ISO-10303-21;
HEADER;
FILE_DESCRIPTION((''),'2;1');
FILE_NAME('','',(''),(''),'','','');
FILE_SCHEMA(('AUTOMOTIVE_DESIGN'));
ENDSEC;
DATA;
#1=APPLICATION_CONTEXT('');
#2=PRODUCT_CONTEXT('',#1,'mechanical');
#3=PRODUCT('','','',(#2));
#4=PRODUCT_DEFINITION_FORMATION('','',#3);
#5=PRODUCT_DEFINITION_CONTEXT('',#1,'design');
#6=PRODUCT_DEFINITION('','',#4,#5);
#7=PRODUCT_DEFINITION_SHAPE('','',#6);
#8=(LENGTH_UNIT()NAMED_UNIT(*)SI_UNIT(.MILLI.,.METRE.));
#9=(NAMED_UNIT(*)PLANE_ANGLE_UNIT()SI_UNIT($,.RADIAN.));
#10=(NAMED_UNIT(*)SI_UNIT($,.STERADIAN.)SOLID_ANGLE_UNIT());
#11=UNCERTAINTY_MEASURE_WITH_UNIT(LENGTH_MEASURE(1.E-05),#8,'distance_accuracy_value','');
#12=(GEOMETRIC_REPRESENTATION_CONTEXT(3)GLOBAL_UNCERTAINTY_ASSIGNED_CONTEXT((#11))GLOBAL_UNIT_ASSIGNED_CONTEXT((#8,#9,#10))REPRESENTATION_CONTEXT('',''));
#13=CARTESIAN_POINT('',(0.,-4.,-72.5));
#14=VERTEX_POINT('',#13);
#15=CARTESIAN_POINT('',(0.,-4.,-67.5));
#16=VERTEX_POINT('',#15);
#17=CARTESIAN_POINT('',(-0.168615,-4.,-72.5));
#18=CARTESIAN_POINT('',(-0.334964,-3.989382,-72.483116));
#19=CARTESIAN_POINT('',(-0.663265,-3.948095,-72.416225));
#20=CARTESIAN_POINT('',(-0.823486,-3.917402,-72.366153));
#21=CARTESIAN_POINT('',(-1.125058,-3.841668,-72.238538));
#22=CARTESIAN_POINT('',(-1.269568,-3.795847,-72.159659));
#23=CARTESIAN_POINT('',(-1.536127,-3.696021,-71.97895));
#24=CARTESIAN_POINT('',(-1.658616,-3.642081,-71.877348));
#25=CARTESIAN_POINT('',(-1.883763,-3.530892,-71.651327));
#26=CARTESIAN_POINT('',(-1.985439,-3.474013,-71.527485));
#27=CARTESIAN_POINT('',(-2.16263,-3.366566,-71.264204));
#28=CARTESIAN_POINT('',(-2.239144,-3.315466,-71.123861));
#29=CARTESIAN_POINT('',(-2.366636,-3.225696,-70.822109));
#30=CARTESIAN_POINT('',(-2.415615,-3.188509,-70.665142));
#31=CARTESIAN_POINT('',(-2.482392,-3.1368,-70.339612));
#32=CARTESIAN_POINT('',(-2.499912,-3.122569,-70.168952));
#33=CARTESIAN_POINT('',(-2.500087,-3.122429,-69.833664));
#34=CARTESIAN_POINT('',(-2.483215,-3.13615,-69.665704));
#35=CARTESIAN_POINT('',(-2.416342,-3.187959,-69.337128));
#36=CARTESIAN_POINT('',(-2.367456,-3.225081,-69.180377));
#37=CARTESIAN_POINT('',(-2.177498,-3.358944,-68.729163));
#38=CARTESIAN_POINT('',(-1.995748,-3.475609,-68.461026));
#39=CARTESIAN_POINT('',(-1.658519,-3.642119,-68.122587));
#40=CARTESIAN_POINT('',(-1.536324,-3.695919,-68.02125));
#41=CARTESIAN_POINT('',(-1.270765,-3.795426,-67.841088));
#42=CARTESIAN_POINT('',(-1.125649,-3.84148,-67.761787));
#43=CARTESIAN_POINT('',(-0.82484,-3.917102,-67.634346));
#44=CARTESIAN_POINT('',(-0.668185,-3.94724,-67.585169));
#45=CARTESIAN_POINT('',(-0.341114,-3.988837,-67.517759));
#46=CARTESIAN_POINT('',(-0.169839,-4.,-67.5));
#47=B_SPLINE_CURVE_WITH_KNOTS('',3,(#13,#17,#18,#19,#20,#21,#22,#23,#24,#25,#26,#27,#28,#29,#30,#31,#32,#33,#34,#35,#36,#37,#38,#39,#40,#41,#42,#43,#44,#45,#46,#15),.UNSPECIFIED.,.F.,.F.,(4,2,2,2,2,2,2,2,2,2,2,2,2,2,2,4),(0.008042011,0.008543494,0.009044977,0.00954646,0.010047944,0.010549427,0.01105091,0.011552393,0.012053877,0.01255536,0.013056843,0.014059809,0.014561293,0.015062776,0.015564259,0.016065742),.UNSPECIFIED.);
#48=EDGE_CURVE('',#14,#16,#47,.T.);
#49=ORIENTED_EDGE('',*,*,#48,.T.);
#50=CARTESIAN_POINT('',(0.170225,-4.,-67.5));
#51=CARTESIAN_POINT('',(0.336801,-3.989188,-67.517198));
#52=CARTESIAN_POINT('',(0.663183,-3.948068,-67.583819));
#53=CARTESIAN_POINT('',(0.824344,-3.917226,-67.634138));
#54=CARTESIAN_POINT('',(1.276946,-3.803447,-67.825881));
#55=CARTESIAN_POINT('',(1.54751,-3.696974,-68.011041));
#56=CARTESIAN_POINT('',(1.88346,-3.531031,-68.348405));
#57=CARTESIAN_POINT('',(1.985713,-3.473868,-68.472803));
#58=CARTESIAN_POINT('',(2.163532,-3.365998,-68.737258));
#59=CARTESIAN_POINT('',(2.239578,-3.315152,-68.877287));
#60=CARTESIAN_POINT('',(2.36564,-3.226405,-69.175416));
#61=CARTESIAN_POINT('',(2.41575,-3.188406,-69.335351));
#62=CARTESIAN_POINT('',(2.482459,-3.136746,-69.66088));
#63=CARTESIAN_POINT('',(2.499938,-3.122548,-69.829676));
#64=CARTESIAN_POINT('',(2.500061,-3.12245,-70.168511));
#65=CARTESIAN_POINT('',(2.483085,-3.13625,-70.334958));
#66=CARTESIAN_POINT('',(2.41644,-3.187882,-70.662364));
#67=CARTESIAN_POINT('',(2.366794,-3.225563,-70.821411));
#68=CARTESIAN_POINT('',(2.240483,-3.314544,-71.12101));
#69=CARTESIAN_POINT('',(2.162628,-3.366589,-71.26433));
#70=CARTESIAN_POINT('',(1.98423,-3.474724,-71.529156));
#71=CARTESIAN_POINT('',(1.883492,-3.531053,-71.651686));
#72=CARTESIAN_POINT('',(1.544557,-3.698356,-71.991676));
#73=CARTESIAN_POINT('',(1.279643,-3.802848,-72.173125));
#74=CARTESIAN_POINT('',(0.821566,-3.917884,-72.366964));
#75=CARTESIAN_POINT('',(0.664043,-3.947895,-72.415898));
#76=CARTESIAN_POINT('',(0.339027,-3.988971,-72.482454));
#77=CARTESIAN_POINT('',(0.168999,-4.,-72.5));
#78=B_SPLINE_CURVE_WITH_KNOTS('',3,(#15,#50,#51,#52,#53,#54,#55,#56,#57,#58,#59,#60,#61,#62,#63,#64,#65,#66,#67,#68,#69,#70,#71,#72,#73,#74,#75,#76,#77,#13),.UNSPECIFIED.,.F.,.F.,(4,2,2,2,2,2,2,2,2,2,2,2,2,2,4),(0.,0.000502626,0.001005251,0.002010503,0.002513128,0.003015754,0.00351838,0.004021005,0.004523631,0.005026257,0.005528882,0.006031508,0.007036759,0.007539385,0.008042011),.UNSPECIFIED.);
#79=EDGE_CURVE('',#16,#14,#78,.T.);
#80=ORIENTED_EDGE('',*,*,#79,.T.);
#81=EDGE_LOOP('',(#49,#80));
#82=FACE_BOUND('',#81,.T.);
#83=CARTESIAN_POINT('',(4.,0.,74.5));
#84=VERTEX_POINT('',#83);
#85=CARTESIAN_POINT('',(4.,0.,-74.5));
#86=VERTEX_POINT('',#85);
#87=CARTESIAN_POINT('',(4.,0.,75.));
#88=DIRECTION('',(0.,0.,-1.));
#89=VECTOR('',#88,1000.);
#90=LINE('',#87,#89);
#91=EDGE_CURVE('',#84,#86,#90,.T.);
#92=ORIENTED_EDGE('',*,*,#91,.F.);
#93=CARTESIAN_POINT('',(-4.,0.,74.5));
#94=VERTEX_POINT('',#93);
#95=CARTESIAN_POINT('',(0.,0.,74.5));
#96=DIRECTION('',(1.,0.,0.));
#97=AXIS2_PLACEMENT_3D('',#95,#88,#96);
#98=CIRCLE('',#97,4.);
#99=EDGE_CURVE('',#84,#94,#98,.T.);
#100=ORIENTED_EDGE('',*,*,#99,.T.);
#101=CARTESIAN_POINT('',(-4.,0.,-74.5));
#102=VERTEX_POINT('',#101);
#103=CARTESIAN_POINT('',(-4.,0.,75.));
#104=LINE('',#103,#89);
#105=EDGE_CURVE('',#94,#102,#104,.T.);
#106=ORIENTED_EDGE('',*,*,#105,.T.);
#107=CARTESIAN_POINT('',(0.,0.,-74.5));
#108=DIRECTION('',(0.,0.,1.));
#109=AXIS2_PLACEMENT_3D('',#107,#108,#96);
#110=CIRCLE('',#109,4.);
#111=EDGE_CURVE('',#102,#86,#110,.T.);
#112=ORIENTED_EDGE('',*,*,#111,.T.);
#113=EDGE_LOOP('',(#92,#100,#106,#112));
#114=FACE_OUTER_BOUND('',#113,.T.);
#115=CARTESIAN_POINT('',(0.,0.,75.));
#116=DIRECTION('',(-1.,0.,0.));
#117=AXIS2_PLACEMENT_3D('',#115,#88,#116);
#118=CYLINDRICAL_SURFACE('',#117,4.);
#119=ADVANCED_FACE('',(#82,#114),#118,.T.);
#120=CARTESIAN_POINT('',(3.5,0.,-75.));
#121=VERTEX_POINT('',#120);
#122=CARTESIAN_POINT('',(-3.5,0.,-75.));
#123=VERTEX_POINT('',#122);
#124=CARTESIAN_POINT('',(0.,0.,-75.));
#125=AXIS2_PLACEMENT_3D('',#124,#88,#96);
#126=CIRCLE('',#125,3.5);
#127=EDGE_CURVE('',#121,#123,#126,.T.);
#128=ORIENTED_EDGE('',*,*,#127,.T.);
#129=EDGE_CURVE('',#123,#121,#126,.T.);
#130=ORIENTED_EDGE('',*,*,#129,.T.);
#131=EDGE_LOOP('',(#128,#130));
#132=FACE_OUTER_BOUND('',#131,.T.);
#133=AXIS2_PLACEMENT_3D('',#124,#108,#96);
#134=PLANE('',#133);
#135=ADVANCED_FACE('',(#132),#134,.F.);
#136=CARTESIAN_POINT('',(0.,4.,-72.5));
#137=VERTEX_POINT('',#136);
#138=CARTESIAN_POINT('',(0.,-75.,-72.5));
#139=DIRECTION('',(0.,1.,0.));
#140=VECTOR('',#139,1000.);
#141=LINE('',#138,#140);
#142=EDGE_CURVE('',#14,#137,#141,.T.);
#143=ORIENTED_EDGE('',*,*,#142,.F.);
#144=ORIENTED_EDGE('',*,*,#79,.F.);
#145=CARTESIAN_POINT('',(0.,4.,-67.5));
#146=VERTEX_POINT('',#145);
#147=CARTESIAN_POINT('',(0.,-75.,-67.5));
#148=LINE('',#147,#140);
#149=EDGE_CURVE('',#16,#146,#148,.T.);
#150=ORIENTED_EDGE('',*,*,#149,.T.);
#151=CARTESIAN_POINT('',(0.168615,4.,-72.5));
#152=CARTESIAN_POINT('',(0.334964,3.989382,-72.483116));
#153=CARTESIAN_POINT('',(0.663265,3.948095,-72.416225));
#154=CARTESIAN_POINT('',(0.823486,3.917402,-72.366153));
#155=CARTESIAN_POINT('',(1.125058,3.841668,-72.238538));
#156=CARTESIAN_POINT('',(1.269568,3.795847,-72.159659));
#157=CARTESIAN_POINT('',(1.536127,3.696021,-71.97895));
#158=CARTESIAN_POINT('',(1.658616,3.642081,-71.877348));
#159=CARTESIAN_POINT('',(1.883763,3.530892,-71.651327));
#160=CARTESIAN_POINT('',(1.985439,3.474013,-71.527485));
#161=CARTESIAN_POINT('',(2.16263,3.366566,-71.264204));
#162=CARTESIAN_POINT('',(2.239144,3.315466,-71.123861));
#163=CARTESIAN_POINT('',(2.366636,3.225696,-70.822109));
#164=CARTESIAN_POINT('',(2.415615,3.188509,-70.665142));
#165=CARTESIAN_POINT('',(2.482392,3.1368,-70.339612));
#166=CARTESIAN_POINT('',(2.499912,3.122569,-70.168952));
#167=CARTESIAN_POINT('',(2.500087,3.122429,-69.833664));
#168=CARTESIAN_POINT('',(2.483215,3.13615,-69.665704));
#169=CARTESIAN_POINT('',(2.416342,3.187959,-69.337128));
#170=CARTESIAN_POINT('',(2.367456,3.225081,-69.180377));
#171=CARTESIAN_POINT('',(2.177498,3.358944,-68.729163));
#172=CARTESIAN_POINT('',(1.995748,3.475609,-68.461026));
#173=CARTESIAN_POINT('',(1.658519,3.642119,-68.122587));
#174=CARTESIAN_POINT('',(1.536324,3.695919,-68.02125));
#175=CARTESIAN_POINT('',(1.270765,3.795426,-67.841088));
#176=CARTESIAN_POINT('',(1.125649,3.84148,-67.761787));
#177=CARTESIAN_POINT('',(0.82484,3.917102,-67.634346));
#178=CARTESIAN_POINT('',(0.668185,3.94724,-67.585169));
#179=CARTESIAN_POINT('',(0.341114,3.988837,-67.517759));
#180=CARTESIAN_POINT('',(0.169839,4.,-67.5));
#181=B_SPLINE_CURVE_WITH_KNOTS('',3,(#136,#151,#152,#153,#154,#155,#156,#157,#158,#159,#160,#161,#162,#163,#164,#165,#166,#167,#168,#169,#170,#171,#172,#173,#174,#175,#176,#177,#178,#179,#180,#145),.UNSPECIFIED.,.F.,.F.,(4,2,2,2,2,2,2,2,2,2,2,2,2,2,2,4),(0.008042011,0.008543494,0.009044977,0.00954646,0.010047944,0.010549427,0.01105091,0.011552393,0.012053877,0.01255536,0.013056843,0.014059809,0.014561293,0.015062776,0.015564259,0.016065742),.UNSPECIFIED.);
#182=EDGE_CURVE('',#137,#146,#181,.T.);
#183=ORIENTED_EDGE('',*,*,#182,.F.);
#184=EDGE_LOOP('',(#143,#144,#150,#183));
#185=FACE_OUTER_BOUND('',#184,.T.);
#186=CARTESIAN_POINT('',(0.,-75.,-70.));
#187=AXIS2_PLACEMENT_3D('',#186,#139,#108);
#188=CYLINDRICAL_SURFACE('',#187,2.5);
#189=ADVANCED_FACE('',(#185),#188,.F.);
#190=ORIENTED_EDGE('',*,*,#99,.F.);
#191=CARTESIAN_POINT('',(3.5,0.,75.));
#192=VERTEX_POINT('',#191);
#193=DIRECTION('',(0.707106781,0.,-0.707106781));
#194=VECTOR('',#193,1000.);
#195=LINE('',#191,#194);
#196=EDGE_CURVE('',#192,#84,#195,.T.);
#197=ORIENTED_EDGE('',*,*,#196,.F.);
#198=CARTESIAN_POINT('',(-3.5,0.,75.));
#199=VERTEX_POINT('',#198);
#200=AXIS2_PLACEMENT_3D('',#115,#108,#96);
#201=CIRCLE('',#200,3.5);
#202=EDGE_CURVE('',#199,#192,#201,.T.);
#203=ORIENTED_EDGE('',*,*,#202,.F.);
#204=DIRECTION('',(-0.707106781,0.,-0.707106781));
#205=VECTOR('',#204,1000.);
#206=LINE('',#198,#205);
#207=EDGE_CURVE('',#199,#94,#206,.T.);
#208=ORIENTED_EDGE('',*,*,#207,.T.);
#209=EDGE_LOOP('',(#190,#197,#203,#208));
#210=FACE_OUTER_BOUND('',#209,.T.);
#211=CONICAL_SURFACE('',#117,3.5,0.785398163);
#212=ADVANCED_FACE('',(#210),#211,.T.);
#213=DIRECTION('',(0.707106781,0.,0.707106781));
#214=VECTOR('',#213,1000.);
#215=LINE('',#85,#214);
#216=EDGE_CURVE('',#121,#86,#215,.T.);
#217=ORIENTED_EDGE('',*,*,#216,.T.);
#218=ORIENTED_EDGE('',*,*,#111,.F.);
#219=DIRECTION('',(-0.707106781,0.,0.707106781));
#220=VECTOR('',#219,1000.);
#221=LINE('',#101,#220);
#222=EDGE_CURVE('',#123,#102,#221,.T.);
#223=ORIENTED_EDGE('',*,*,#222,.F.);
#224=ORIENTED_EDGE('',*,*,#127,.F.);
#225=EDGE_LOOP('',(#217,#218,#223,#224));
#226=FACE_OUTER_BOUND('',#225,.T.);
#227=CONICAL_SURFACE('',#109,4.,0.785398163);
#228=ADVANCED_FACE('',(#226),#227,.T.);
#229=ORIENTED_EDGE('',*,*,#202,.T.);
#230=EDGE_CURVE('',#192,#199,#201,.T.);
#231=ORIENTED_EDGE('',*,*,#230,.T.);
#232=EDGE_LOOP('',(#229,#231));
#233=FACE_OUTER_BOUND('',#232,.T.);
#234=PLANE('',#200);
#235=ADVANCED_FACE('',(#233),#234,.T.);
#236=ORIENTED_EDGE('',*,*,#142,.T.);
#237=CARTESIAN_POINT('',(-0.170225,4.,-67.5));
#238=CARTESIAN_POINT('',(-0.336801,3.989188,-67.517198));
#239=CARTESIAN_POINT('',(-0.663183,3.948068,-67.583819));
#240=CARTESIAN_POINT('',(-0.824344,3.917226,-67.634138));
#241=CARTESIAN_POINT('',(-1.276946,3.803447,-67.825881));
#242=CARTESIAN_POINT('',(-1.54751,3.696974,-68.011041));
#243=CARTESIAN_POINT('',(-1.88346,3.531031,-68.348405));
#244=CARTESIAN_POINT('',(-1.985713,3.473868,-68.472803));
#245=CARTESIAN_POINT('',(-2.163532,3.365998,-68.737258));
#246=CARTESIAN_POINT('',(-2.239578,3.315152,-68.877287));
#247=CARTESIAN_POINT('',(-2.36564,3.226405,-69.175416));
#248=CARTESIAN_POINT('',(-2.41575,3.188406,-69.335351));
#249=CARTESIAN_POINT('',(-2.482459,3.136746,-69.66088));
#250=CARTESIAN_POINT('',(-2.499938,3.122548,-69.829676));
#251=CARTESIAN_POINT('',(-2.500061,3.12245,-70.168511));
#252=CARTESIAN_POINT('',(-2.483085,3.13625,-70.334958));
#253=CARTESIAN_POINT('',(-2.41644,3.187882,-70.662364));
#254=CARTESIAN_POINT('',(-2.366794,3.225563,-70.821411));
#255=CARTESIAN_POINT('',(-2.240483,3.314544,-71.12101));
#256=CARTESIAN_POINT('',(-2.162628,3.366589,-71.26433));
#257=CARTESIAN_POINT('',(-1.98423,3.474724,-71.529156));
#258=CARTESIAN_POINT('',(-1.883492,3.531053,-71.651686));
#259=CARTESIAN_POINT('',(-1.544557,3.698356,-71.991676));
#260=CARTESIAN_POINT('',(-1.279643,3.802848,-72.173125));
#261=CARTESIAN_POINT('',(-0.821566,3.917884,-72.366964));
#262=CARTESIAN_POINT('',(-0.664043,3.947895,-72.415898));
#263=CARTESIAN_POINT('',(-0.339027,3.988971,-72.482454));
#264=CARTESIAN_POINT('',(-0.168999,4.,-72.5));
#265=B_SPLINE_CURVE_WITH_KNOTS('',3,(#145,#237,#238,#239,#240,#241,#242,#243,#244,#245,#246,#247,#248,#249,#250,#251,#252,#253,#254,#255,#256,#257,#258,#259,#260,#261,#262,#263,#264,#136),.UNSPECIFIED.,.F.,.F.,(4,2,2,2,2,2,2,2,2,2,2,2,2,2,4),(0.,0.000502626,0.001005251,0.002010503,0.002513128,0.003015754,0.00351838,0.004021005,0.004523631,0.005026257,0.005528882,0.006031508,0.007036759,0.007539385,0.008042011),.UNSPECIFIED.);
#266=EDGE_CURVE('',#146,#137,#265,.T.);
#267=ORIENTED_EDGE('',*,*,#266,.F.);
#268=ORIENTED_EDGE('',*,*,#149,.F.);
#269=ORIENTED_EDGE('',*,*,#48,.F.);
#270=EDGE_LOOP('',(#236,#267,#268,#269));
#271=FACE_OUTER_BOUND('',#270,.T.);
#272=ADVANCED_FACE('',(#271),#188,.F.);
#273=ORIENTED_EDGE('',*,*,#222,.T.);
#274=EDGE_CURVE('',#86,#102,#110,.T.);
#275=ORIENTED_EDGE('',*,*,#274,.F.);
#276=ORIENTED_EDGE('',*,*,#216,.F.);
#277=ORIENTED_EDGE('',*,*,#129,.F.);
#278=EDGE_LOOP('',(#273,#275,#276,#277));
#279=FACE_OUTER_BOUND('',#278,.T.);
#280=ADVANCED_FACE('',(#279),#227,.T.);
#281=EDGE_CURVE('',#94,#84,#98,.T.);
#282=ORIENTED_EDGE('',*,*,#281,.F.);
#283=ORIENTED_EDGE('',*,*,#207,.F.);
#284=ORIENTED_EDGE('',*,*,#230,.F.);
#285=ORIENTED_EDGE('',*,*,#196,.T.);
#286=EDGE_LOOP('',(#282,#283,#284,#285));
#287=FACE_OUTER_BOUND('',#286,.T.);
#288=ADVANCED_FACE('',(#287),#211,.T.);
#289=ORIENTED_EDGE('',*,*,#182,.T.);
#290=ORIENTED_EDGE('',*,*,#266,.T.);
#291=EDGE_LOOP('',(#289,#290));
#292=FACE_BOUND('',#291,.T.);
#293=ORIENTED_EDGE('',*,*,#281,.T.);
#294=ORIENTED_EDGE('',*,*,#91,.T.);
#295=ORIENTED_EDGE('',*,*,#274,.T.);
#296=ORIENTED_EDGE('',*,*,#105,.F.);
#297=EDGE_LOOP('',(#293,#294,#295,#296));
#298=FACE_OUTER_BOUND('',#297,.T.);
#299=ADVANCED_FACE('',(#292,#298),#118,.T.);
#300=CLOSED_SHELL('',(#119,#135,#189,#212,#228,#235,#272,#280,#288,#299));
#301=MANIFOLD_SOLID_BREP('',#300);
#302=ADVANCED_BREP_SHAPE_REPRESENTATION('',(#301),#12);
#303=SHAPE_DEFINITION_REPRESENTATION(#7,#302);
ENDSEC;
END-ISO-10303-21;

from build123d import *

# Parameters (mm, degrees)
SKETCH1_R           = 4
BOSS_EXTRUDE1_DEPTH = 75
SKETCH2_R           = 2.5
CUT_EXTRUDE1_DEPTH  = 75
CHAMFER1_SIZE       = 0.5


with BuildPart() as part:
    # Sketch1 → Boss-Extrude1 (new, symmetric)
    with BuildSketch(Plane.XY):
        Circle(SKETCH1_R)
    extrude(amount=BOSS_EXTRUDE1_DEPTH, both=True)

    # Sketch2 → Cut-Extrude1 (cut, symmetric)
    with BuildSketch(Plane(origin=(0, 0, 0), x_dir=(1, 0, 0), z_dir=(0, 1, 0))):
        with Locations(Location((0, 70, 0), (0, 0, 270))):
            Circle(SKETCH2_R)
    extrude(amount=CUT_EXTRUDE1_DEPTH, both=True, mode=Mode.SUBTRACT)

    # Chamfer1
    chamfer1_edges = [part.edges().sort_by_distance(p)[0] for p in [
        (-4, 0, -75),
        (-4, 0, 75),
    ]]
    chamfer(chamfer1_edges, length=CHAMFER1_SIZE)


solid = part.part
